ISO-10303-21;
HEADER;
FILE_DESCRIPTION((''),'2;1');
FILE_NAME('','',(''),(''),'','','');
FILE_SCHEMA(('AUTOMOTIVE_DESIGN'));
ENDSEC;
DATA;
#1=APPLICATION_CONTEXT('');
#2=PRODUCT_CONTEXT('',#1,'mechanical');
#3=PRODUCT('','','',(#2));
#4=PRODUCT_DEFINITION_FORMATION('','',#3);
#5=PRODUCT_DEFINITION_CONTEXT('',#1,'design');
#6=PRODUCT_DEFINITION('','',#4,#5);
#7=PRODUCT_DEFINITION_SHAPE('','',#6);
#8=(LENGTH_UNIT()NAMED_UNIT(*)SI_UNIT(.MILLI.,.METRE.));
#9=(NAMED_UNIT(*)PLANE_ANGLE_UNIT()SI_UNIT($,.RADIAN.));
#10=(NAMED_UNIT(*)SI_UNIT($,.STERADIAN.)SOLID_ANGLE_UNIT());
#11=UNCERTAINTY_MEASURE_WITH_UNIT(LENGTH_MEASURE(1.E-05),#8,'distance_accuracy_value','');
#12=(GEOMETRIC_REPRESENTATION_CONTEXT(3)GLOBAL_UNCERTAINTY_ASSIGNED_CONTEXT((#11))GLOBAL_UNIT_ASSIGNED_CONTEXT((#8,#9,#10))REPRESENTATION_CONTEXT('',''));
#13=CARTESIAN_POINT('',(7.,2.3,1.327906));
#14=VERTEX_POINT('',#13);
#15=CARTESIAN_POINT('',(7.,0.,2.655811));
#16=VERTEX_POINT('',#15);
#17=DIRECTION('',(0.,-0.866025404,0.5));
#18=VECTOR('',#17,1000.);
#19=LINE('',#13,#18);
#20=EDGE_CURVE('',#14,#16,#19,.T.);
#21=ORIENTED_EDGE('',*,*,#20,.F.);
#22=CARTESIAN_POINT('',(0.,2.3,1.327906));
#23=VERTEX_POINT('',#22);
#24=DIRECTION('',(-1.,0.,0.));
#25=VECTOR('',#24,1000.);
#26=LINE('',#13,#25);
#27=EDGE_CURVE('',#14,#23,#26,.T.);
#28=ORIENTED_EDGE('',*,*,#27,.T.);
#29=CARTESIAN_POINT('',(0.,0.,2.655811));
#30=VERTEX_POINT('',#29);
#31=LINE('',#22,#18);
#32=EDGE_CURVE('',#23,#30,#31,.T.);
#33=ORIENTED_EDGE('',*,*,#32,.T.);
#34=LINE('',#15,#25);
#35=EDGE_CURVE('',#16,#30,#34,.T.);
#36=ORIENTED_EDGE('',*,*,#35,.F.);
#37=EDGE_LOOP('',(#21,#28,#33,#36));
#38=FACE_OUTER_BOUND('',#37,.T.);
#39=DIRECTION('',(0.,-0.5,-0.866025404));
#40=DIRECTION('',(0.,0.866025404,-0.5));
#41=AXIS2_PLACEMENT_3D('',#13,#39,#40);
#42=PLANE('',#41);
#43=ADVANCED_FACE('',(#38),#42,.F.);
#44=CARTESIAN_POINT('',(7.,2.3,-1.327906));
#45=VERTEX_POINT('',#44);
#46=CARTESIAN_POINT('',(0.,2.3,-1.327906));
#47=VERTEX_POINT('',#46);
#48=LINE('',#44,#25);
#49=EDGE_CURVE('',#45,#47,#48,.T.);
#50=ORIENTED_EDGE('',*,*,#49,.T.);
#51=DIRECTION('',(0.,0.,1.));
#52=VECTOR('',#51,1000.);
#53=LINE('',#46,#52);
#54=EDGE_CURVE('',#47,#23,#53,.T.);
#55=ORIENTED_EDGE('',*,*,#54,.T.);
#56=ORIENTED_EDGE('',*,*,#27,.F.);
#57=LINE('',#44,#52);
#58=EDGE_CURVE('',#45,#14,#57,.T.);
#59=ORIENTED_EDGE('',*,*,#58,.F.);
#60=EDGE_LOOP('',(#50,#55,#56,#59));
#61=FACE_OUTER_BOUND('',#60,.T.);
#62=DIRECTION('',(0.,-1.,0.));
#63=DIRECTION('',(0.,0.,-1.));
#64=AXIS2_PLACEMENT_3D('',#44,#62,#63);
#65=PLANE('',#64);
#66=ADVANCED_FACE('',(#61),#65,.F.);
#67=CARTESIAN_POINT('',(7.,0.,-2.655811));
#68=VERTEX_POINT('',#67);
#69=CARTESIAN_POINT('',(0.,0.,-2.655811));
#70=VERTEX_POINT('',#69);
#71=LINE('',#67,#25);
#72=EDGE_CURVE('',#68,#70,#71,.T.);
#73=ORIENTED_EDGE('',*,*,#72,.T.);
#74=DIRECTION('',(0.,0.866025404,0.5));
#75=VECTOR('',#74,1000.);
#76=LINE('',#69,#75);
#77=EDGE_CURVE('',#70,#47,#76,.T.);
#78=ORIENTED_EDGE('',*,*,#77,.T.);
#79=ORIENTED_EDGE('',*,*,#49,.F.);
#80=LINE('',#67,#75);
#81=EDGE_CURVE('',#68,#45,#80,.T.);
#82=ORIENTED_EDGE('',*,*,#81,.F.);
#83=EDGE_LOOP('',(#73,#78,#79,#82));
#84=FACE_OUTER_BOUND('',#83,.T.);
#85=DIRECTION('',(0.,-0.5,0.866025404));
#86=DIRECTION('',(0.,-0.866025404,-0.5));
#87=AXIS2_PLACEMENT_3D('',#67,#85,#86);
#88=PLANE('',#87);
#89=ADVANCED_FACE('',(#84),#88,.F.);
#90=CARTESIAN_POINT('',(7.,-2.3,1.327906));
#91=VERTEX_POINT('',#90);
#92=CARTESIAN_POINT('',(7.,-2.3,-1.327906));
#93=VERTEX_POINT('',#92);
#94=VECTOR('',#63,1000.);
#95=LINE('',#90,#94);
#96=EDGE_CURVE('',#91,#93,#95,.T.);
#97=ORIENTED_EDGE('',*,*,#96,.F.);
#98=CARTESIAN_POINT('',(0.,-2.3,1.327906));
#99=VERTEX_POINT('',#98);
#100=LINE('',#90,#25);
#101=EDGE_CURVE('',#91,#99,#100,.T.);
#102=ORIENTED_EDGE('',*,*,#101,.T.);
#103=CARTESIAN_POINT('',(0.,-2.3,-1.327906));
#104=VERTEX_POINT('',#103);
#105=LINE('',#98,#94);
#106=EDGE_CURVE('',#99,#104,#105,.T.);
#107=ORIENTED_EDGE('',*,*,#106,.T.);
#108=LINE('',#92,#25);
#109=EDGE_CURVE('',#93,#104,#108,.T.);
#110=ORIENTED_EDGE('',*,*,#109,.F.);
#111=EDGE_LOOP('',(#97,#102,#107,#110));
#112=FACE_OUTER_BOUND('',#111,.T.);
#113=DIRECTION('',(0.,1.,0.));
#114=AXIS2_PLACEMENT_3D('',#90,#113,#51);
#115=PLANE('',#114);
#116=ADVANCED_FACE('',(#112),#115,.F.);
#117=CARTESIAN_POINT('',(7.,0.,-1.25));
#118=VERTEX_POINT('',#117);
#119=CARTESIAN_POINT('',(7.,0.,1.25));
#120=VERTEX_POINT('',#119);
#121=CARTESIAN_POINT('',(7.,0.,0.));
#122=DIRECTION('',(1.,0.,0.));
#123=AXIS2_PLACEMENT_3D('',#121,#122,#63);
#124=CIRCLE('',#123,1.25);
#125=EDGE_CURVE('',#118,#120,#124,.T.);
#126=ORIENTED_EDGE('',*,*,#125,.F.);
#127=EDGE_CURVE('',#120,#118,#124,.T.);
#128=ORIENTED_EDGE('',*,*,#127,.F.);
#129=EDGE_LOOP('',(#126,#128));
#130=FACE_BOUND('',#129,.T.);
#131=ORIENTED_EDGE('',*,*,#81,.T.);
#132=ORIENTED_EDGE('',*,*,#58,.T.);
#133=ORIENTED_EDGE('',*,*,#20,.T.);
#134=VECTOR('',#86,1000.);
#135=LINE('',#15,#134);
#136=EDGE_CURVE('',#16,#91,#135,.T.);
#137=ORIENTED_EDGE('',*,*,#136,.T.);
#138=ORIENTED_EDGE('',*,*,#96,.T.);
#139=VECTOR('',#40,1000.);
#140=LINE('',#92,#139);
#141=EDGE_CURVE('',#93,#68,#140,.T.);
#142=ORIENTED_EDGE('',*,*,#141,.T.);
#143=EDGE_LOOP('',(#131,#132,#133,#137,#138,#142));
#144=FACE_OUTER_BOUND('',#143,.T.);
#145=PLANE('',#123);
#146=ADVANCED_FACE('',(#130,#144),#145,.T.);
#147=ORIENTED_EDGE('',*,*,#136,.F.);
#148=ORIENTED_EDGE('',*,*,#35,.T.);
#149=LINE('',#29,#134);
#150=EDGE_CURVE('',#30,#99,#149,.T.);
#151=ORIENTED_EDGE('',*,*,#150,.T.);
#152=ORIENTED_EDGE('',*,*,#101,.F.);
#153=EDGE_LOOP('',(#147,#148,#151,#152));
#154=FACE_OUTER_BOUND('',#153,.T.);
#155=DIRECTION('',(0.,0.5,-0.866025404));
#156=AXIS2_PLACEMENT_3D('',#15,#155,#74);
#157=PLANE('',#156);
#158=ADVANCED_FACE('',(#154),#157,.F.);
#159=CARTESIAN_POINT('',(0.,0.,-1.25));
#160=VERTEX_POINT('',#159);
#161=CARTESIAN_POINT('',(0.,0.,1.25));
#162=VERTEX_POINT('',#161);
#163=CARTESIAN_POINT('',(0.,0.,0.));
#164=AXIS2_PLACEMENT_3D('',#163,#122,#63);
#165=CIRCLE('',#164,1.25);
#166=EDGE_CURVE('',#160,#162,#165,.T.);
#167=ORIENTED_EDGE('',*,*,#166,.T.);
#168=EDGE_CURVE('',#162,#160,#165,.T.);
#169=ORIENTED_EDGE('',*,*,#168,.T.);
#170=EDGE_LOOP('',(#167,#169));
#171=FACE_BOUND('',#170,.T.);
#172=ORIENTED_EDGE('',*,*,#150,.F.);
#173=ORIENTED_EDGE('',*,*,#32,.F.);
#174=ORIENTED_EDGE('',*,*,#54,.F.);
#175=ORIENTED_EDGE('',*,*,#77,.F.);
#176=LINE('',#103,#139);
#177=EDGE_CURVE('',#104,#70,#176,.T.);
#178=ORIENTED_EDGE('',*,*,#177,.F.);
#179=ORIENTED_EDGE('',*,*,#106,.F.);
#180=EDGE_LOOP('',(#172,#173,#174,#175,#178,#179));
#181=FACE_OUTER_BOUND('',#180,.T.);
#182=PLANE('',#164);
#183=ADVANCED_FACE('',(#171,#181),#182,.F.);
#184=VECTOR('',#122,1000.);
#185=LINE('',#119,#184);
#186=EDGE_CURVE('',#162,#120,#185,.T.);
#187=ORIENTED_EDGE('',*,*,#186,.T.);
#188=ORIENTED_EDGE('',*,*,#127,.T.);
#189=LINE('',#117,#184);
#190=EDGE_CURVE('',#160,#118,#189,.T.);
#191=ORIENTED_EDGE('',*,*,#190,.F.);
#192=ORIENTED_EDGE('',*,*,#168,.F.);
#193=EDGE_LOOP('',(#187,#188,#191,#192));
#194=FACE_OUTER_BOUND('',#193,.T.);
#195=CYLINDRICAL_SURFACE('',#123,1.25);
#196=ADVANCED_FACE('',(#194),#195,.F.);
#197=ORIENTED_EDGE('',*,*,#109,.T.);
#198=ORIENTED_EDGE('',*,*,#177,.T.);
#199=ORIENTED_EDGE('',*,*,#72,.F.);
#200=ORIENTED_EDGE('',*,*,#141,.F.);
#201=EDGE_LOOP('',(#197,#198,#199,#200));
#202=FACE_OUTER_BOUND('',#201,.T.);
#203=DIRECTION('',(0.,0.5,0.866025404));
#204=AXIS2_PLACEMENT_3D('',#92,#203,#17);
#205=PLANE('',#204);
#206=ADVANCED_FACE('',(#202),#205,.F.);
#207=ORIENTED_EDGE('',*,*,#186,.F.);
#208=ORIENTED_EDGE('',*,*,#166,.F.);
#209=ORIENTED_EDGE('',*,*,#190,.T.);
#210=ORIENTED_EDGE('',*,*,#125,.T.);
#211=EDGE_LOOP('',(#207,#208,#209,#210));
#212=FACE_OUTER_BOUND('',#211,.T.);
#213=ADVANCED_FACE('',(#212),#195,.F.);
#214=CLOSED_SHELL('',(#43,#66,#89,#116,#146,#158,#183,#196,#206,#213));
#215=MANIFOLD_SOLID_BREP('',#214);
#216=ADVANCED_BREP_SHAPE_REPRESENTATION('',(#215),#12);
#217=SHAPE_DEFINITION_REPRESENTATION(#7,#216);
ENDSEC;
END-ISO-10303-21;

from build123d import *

# Parameters (mm, degrees)
EXTRUDE_1_DEPTH    = 7
HOLE_WIZARD_M3_1_D = 2.5


with BuildPart() as part:
    # 草图1 → 凸台-拉伸1 (new body)
    with BuildSketch(Plane(origin=(0, 0, 0), x_dir=(0, 0, -1), z_dir=(1, 0, 0))):
        Polygon((2.655811238, 0), (1.327905619, 2.3), (-1.327905619, 2.3), (-2.655811238, 0), (-1.327905619, -2.3), (1.327905619, -2.3), align=None)
    extrude(amount=EXTRUDE_1_DEPTH)

    # M3 螺纹孔1 (through all)
    with Locations(Plane(origin=(7, 0, 0), x_dir=(0, 0, -1), z_dir=(1, 0, 0))):
        with Locations((0, 0)):
            Hole(HOLE_WIZARD_M3_1_D / 2)


solid = part.part
